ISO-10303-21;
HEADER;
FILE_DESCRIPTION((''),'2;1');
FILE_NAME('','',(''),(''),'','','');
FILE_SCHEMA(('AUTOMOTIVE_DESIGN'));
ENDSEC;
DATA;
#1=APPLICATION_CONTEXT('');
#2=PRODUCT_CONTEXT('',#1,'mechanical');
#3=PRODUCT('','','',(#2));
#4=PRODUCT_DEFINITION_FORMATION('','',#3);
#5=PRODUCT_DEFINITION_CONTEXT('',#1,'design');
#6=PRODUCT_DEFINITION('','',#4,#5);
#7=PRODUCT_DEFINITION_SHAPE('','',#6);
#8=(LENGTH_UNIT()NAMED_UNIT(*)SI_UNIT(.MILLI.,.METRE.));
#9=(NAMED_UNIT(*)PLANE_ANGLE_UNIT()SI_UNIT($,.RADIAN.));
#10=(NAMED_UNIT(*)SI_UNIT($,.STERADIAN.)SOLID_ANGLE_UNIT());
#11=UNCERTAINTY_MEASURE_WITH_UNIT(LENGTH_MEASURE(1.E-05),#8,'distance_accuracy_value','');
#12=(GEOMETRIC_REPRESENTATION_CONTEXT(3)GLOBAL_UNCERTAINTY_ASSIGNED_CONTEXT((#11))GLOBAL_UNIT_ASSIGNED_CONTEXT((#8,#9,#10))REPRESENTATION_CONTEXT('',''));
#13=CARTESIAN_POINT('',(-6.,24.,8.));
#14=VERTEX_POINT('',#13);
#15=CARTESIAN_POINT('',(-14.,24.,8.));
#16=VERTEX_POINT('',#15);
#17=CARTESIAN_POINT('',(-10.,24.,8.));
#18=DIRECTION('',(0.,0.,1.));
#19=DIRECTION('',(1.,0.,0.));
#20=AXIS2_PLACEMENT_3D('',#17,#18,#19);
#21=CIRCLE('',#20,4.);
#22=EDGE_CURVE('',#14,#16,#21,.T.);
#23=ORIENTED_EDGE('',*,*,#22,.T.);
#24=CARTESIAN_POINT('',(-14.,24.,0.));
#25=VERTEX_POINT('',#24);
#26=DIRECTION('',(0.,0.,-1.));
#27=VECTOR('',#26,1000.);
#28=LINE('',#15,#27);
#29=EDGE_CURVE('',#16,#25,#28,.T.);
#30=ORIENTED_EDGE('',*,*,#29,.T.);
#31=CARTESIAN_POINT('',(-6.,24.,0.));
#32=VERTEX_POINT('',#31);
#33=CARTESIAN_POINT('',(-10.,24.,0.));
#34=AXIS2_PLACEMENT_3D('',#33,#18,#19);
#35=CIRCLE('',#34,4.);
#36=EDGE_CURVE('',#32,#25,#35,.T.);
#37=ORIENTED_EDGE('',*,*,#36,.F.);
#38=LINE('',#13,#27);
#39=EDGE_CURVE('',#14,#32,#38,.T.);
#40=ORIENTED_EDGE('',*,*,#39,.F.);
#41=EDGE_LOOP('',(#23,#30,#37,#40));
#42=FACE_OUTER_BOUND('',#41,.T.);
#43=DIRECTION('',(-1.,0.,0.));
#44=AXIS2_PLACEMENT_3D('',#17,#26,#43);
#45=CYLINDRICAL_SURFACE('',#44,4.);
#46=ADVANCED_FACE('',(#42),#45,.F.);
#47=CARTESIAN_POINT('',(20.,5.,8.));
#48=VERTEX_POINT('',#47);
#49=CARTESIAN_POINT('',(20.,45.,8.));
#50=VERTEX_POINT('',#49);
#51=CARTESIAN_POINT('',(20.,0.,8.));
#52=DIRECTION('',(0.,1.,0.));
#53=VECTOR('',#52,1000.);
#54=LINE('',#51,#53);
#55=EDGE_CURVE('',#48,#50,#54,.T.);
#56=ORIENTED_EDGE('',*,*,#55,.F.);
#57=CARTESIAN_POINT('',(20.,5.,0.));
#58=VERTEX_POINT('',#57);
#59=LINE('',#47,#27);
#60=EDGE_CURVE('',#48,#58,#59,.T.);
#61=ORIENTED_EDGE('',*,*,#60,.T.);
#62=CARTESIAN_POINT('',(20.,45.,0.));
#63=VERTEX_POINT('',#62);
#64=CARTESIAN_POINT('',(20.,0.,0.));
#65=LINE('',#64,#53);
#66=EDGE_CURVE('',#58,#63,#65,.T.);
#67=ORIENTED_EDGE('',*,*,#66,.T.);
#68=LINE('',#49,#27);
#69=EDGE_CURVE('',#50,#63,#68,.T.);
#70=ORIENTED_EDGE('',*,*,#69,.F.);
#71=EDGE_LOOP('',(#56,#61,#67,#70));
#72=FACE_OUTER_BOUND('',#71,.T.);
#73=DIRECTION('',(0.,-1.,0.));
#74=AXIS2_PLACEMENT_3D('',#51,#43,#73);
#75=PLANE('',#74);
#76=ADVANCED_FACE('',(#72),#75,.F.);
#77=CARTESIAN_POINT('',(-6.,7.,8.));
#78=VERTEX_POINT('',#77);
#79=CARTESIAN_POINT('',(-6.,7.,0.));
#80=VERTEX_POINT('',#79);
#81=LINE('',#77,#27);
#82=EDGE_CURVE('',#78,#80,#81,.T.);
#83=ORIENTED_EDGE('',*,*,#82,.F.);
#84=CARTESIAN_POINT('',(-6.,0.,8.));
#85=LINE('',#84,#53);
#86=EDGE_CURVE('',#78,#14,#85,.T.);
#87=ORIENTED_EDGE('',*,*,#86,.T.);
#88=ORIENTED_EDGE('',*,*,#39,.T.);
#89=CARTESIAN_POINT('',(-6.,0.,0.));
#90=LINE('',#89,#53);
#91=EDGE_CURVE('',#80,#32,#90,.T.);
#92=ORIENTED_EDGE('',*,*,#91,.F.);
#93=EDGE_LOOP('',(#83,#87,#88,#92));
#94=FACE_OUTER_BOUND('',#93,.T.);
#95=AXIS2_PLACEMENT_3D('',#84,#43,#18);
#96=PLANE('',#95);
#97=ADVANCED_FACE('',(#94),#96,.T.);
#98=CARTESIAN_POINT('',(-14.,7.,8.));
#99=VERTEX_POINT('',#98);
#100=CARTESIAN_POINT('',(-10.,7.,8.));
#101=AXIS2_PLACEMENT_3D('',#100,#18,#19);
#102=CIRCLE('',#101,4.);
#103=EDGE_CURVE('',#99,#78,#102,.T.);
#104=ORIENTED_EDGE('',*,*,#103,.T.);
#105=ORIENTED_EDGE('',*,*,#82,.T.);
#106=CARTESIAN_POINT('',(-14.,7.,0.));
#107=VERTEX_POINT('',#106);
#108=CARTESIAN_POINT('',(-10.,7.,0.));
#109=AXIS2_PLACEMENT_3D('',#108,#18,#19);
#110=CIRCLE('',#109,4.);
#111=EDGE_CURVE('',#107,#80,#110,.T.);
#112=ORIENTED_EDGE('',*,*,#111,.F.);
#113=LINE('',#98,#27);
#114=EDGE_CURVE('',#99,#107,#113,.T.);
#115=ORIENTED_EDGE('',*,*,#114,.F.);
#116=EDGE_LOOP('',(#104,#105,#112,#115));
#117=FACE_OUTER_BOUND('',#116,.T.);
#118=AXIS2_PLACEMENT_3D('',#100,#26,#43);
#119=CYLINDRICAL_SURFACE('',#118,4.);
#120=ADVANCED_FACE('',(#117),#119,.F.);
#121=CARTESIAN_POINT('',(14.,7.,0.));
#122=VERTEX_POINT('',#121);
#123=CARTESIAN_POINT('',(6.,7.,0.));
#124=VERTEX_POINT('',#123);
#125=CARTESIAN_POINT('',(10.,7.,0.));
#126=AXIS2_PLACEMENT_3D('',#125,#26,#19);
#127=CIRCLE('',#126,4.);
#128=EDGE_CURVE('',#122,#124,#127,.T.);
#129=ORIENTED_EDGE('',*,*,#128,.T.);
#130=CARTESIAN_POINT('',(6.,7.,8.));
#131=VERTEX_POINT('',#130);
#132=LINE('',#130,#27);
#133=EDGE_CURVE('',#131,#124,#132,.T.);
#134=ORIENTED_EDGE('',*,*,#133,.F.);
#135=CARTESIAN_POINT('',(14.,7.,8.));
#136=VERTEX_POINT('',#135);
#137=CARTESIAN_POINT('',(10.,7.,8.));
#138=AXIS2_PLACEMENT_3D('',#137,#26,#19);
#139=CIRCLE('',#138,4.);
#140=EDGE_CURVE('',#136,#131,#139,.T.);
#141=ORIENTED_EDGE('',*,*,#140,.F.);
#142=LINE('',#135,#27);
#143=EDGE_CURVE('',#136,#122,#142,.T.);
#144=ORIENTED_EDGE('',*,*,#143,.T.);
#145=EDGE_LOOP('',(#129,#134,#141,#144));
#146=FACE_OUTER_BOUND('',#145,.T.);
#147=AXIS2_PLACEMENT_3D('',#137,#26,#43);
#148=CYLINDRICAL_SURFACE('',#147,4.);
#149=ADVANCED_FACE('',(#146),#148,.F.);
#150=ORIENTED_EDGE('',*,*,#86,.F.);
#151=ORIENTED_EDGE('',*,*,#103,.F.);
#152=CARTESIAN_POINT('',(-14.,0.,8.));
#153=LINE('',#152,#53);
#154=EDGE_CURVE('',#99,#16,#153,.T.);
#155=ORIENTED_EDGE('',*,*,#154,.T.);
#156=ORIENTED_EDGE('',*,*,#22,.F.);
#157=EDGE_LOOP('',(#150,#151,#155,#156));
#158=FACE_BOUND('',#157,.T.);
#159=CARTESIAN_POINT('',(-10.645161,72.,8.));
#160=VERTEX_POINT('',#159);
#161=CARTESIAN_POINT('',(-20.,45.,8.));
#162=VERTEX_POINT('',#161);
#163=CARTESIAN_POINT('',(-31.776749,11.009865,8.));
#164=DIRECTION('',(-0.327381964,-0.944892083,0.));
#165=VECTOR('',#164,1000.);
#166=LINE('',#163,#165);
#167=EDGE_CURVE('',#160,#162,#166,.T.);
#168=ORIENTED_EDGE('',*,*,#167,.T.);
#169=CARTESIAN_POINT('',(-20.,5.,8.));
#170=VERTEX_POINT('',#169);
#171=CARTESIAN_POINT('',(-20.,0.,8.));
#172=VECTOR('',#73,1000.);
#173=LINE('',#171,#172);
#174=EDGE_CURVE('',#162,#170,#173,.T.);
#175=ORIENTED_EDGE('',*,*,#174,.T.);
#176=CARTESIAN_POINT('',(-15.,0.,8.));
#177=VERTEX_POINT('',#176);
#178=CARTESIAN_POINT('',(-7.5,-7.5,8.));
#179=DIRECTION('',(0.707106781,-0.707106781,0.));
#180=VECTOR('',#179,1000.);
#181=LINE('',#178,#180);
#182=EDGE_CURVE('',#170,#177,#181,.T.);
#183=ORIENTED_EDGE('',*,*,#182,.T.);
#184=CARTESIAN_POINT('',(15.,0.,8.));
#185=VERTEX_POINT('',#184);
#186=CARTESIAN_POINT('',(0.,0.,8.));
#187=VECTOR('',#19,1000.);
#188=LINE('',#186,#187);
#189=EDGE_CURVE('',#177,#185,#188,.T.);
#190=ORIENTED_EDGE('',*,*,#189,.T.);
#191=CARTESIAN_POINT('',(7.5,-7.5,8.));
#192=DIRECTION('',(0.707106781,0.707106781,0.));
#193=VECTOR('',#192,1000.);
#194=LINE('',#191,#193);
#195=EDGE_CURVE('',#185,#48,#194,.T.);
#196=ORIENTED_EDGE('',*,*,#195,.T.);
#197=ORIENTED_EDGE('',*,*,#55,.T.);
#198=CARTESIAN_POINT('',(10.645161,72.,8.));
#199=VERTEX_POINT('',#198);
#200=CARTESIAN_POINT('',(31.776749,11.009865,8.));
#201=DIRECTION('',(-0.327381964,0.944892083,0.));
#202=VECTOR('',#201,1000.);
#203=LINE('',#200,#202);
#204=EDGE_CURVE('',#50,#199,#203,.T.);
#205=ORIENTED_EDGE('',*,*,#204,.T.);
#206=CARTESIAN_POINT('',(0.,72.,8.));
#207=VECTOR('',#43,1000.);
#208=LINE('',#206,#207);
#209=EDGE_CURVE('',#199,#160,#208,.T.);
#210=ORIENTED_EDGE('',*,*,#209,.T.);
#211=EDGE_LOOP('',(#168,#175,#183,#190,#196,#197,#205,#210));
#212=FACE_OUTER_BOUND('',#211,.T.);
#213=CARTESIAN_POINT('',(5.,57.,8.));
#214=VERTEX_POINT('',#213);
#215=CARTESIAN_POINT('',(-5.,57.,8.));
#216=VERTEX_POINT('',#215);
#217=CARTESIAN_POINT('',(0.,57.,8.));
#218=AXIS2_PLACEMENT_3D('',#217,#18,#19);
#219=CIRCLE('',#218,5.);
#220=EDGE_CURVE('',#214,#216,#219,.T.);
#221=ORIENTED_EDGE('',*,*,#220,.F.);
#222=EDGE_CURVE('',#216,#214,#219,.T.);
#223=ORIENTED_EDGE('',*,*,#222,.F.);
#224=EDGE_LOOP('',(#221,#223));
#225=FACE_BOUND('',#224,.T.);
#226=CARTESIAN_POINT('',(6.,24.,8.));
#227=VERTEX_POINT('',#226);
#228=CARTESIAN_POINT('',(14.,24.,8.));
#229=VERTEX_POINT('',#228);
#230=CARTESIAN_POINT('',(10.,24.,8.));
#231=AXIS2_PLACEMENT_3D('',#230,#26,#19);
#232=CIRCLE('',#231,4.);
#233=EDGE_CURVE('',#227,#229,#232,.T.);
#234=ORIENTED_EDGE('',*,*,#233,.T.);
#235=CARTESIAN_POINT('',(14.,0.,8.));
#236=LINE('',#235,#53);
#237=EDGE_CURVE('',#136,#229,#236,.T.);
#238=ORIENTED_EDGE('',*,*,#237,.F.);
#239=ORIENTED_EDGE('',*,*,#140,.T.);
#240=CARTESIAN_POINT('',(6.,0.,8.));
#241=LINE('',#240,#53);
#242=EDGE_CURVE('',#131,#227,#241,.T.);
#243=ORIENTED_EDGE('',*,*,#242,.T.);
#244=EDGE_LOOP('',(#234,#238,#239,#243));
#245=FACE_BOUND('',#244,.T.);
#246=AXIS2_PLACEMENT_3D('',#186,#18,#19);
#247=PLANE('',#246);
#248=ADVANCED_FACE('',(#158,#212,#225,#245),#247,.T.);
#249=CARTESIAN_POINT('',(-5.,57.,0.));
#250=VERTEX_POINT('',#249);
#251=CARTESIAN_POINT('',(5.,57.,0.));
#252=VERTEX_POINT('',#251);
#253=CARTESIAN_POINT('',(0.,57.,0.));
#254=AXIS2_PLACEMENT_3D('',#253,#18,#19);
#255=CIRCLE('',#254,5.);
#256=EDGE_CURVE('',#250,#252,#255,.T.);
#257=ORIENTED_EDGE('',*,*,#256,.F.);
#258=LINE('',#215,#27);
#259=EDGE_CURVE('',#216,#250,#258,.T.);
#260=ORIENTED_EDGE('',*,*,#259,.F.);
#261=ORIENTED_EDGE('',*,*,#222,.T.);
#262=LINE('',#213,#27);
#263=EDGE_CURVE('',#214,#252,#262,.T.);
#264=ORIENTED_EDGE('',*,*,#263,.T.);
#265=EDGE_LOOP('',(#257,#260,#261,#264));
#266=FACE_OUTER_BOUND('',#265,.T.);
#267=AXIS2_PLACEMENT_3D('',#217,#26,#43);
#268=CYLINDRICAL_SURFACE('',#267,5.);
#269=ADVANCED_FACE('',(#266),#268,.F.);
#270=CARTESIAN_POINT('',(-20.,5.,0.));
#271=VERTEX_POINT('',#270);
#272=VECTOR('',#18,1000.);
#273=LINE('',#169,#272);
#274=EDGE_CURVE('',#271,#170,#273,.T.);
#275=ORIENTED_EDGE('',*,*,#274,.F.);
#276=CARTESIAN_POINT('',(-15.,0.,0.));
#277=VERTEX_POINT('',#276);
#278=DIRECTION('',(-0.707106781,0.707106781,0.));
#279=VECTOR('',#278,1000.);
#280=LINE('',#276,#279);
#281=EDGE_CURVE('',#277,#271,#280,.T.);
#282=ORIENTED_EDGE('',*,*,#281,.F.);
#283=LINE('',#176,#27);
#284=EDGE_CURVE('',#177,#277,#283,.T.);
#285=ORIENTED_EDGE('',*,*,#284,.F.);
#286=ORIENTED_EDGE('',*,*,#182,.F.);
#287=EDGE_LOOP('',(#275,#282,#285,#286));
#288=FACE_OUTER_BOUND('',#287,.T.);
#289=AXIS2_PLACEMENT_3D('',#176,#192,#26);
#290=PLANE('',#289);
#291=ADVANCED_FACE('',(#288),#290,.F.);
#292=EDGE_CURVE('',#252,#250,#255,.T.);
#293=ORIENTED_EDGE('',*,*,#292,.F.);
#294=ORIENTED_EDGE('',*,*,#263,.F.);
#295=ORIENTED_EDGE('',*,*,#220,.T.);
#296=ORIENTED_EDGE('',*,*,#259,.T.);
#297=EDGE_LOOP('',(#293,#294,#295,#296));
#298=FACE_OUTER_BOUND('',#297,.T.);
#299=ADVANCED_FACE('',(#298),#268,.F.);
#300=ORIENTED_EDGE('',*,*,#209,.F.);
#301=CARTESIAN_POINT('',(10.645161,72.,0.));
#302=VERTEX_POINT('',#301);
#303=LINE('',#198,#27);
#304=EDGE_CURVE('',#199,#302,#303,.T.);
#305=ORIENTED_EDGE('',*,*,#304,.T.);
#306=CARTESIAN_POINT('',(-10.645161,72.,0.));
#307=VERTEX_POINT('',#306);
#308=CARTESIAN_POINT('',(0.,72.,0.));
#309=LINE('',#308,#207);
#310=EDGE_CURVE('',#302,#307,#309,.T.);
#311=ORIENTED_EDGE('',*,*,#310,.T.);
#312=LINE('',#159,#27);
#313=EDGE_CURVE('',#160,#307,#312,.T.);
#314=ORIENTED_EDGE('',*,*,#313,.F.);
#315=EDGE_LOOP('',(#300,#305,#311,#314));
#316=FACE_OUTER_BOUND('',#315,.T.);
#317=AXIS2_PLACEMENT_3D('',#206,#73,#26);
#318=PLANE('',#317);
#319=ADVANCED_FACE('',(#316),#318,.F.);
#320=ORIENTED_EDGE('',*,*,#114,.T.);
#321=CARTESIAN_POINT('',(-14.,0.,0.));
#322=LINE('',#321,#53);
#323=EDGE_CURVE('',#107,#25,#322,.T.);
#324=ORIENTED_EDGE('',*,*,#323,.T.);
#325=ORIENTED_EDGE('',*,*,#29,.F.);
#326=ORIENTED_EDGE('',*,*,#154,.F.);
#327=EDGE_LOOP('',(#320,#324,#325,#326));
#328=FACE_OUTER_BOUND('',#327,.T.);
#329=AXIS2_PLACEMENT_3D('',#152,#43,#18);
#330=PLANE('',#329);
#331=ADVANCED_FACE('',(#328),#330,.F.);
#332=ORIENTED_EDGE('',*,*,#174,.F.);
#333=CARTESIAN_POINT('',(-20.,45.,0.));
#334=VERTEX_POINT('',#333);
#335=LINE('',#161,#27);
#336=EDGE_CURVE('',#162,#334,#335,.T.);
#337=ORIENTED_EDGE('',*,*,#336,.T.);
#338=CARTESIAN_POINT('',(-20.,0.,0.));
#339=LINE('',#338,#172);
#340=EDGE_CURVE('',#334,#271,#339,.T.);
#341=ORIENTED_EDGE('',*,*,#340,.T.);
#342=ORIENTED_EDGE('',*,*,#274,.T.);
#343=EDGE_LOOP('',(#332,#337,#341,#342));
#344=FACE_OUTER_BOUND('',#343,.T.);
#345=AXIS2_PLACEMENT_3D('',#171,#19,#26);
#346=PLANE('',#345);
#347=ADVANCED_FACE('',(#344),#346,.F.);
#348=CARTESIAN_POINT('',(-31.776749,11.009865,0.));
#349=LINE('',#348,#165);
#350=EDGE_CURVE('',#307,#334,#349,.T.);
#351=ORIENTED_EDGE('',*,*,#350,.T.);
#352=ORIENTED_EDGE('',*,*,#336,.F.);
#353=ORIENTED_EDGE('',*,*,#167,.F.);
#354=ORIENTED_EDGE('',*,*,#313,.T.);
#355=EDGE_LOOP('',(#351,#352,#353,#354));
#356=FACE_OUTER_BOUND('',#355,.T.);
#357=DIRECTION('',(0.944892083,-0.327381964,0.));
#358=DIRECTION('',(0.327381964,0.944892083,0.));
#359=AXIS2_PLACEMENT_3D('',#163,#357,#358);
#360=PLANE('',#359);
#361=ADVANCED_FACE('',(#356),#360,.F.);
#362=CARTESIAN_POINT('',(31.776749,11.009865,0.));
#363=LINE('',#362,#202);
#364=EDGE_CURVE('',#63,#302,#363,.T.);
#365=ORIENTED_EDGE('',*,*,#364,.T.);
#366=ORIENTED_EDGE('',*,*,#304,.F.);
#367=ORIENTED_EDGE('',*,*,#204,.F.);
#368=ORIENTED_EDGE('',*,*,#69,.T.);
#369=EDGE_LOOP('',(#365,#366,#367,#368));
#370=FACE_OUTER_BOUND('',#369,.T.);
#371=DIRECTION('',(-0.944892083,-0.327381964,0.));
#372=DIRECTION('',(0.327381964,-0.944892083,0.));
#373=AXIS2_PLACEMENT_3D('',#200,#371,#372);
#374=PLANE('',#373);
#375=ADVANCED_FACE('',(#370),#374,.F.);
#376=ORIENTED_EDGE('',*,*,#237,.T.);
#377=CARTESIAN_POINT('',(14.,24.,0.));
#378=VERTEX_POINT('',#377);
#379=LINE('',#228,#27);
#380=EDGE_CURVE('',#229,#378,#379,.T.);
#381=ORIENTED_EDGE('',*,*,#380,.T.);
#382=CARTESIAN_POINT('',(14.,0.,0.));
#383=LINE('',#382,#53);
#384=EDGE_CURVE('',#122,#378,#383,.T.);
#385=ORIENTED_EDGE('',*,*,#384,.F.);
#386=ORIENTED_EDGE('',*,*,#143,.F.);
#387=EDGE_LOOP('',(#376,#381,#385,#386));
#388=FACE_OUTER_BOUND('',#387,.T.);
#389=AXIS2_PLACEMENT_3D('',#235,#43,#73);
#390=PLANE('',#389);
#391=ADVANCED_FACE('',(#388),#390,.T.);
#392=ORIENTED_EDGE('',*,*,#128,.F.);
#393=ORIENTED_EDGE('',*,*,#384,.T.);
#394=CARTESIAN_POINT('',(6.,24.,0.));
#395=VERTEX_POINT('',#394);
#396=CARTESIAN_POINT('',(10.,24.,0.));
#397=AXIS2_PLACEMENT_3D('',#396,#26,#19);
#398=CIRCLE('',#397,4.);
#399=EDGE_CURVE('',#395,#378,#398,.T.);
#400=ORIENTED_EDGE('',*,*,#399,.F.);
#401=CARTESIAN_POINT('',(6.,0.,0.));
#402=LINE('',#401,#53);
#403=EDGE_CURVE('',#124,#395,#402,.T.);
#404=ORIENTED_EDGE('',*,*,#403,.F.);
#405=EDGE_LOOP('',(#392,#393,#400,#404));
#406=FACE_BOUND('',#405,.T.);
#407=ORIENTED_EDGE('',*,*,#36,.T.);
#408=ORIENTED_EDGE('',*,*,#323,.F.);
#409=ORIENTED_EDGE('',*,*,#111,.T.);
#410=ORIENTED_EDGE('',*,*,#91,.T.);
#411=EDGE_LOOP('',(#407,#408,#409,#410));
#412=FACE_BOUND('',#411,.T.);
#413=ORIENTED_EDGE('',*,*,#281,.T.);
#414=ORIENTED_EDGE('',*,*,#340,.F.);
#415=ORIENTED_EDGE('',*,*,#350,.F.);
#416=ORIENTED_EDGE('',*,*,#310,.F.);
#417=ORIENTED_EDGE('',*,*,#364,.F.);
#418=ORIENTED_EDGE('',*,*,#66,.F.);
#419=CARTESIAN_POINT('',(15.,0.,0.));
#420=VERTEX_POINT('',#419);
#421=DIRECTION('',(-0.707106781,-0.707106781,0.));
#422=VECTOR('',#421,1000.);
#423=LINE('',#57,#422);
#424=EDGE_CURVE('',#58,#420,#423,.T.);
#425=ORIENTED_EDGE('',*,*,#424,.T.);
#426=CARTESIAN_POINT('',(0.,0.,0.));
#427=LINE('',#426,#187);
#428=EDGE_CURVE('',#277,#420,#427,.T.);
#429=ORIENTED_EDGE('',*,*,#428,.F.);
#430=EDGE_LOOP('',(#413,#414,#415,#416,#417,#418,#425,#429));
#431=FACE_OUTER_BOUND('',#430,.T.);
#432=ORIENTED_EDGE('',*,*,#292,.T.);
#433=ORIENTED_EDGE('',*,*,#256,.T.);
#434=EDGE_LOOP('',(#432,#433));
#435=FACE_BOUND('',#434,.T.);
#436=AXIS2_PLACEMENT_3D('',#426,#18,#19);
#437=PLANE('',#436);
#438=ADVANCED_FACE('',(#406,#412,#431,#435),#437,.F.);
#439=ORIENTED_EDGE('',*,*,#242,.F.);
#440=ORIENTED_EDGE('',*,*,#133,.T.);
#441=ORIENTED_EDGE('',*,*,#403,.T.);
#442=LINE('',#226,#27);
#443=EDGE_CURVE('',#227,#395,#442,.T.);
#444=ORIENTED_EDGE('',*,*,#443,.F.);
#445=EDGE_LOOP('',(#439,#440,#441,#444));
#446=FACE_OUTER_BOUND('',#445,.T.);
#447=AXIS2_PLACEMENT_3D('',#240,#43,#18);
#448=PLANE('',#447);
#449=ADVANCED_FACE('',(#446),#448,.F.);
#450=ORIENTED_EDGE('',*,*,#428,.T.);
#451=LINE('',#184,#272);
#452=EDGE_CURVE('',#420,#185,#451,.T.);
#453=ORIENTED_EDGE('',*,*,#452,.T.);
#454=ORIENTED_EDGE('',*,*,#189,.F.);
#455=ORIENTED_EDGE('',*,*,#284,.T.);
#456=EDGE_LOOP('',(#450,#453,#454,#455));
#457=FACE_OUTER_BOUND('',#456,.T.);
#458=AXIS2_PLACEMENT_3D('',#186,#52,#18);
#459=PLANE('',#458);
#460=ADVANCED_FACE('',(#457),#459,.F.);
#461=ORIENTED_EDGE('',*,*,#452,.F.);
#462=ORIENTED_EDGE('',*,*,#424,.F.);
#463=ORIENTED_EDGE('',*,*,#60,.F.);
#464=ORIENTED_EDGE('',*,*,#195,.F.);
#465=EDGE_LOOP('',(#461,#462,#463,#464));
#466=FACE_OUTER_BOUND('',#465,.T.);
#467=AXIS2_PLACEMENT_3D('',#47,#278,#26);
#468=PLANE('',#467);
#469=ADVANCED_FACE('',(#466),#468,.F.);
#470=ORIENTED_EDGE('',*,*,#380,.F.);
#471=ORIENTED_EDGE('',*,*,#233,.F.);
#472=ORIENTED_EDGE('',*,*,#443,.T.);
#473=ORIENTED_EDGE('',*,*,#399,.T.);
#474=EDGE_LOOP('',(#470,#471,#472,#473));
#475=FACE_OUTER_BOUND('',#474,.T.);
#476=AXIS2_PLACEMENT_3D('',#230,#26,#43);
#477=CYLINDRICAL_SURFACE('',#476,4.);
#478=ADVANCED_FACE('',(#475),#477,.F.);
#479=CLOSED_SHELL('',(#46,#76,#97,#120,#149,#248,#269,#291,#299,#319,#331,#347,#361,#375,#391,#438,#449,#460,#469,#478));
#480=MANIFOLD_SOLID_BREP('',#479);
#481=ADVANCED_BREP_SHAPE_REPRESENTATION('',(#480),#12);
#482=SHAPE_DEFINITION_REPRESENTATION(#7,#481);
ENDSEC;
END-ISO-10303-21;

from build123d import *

# Parameters (mm, degrees)
EXTRUDE_1_DEPTH = 8
CHAMFER_1_SIZE  = 5


with BuildPart() as part:
    # 草图1 → 凸台-拉伸1 (new body)
    # profile 1 of 2: a face of its own
    with BuildSketch(Plane.XY):
        with BuildLine():
            Line((-20, 45), (-20, 0))
            Line((-20, 0), (0, 0))
            Line((0, 0), (0, 52))
            ThreePointArc((0, 52), (-5, 57), (0, 62))
            Line((0, 62), (0, 72))
            Line((0, 72), (-10.64516129, 72))
            Line((-10.64516129, 72), (-20, 45))
        make_face()
        with BuildLine():
            ThreePointArc((-6, 7), (-10, 3), (-14, 7))
            Line((-14, 7), (-14, 24))
            ThreePointArc((-14, 24), (-10, 28), (-6, 24))
            Line((-6, 24), (-6, 7))
        make_face(mode=Mode.SUBTRACT)
    # profile 2 of 2: a face of its own
    with BuildSketch(Plane.XY):
        with BuildLine():
            Line((0, 52), (0, 0))
            Line((0, 0), (20, 0))
            Line((20, 0), (20, 45))
            Line((20, 45), (10.64516129, 72))
            Line((10.64516129, 72), (0, 72))
            Line((0, 72), (0, 62))
            ThreePointArc((0, 62), (3.535533906, 60.535533906), (5, 57))
            ThreePointArc((5, 57), (3.535533906, 53.464466094), (0, 52))
        make_face()
        with BuildLine():
            ThreePointArc((14, 7), (10, 3), (6, 7))
            Line((6, 7), (6, 24))
            ThreePointArc((6, 24), (10, 28), (14, 24))
            Line((14, 24), (14, 7))
        make_face(mode=Mode.SUBTRACT)
    extrude(amount=EXTRUDE_1_DEPTH)

    # 倒角1
    chamfer_1_edges = [part.edges().sort_by_distance(p)[0] for p in [
        (-20, 0, 4),
        (20, 0, 4),
    ]]
    chamfer(chamfer_1_edges, length=CHAMFER_1_SIZE)


solid = part.part
